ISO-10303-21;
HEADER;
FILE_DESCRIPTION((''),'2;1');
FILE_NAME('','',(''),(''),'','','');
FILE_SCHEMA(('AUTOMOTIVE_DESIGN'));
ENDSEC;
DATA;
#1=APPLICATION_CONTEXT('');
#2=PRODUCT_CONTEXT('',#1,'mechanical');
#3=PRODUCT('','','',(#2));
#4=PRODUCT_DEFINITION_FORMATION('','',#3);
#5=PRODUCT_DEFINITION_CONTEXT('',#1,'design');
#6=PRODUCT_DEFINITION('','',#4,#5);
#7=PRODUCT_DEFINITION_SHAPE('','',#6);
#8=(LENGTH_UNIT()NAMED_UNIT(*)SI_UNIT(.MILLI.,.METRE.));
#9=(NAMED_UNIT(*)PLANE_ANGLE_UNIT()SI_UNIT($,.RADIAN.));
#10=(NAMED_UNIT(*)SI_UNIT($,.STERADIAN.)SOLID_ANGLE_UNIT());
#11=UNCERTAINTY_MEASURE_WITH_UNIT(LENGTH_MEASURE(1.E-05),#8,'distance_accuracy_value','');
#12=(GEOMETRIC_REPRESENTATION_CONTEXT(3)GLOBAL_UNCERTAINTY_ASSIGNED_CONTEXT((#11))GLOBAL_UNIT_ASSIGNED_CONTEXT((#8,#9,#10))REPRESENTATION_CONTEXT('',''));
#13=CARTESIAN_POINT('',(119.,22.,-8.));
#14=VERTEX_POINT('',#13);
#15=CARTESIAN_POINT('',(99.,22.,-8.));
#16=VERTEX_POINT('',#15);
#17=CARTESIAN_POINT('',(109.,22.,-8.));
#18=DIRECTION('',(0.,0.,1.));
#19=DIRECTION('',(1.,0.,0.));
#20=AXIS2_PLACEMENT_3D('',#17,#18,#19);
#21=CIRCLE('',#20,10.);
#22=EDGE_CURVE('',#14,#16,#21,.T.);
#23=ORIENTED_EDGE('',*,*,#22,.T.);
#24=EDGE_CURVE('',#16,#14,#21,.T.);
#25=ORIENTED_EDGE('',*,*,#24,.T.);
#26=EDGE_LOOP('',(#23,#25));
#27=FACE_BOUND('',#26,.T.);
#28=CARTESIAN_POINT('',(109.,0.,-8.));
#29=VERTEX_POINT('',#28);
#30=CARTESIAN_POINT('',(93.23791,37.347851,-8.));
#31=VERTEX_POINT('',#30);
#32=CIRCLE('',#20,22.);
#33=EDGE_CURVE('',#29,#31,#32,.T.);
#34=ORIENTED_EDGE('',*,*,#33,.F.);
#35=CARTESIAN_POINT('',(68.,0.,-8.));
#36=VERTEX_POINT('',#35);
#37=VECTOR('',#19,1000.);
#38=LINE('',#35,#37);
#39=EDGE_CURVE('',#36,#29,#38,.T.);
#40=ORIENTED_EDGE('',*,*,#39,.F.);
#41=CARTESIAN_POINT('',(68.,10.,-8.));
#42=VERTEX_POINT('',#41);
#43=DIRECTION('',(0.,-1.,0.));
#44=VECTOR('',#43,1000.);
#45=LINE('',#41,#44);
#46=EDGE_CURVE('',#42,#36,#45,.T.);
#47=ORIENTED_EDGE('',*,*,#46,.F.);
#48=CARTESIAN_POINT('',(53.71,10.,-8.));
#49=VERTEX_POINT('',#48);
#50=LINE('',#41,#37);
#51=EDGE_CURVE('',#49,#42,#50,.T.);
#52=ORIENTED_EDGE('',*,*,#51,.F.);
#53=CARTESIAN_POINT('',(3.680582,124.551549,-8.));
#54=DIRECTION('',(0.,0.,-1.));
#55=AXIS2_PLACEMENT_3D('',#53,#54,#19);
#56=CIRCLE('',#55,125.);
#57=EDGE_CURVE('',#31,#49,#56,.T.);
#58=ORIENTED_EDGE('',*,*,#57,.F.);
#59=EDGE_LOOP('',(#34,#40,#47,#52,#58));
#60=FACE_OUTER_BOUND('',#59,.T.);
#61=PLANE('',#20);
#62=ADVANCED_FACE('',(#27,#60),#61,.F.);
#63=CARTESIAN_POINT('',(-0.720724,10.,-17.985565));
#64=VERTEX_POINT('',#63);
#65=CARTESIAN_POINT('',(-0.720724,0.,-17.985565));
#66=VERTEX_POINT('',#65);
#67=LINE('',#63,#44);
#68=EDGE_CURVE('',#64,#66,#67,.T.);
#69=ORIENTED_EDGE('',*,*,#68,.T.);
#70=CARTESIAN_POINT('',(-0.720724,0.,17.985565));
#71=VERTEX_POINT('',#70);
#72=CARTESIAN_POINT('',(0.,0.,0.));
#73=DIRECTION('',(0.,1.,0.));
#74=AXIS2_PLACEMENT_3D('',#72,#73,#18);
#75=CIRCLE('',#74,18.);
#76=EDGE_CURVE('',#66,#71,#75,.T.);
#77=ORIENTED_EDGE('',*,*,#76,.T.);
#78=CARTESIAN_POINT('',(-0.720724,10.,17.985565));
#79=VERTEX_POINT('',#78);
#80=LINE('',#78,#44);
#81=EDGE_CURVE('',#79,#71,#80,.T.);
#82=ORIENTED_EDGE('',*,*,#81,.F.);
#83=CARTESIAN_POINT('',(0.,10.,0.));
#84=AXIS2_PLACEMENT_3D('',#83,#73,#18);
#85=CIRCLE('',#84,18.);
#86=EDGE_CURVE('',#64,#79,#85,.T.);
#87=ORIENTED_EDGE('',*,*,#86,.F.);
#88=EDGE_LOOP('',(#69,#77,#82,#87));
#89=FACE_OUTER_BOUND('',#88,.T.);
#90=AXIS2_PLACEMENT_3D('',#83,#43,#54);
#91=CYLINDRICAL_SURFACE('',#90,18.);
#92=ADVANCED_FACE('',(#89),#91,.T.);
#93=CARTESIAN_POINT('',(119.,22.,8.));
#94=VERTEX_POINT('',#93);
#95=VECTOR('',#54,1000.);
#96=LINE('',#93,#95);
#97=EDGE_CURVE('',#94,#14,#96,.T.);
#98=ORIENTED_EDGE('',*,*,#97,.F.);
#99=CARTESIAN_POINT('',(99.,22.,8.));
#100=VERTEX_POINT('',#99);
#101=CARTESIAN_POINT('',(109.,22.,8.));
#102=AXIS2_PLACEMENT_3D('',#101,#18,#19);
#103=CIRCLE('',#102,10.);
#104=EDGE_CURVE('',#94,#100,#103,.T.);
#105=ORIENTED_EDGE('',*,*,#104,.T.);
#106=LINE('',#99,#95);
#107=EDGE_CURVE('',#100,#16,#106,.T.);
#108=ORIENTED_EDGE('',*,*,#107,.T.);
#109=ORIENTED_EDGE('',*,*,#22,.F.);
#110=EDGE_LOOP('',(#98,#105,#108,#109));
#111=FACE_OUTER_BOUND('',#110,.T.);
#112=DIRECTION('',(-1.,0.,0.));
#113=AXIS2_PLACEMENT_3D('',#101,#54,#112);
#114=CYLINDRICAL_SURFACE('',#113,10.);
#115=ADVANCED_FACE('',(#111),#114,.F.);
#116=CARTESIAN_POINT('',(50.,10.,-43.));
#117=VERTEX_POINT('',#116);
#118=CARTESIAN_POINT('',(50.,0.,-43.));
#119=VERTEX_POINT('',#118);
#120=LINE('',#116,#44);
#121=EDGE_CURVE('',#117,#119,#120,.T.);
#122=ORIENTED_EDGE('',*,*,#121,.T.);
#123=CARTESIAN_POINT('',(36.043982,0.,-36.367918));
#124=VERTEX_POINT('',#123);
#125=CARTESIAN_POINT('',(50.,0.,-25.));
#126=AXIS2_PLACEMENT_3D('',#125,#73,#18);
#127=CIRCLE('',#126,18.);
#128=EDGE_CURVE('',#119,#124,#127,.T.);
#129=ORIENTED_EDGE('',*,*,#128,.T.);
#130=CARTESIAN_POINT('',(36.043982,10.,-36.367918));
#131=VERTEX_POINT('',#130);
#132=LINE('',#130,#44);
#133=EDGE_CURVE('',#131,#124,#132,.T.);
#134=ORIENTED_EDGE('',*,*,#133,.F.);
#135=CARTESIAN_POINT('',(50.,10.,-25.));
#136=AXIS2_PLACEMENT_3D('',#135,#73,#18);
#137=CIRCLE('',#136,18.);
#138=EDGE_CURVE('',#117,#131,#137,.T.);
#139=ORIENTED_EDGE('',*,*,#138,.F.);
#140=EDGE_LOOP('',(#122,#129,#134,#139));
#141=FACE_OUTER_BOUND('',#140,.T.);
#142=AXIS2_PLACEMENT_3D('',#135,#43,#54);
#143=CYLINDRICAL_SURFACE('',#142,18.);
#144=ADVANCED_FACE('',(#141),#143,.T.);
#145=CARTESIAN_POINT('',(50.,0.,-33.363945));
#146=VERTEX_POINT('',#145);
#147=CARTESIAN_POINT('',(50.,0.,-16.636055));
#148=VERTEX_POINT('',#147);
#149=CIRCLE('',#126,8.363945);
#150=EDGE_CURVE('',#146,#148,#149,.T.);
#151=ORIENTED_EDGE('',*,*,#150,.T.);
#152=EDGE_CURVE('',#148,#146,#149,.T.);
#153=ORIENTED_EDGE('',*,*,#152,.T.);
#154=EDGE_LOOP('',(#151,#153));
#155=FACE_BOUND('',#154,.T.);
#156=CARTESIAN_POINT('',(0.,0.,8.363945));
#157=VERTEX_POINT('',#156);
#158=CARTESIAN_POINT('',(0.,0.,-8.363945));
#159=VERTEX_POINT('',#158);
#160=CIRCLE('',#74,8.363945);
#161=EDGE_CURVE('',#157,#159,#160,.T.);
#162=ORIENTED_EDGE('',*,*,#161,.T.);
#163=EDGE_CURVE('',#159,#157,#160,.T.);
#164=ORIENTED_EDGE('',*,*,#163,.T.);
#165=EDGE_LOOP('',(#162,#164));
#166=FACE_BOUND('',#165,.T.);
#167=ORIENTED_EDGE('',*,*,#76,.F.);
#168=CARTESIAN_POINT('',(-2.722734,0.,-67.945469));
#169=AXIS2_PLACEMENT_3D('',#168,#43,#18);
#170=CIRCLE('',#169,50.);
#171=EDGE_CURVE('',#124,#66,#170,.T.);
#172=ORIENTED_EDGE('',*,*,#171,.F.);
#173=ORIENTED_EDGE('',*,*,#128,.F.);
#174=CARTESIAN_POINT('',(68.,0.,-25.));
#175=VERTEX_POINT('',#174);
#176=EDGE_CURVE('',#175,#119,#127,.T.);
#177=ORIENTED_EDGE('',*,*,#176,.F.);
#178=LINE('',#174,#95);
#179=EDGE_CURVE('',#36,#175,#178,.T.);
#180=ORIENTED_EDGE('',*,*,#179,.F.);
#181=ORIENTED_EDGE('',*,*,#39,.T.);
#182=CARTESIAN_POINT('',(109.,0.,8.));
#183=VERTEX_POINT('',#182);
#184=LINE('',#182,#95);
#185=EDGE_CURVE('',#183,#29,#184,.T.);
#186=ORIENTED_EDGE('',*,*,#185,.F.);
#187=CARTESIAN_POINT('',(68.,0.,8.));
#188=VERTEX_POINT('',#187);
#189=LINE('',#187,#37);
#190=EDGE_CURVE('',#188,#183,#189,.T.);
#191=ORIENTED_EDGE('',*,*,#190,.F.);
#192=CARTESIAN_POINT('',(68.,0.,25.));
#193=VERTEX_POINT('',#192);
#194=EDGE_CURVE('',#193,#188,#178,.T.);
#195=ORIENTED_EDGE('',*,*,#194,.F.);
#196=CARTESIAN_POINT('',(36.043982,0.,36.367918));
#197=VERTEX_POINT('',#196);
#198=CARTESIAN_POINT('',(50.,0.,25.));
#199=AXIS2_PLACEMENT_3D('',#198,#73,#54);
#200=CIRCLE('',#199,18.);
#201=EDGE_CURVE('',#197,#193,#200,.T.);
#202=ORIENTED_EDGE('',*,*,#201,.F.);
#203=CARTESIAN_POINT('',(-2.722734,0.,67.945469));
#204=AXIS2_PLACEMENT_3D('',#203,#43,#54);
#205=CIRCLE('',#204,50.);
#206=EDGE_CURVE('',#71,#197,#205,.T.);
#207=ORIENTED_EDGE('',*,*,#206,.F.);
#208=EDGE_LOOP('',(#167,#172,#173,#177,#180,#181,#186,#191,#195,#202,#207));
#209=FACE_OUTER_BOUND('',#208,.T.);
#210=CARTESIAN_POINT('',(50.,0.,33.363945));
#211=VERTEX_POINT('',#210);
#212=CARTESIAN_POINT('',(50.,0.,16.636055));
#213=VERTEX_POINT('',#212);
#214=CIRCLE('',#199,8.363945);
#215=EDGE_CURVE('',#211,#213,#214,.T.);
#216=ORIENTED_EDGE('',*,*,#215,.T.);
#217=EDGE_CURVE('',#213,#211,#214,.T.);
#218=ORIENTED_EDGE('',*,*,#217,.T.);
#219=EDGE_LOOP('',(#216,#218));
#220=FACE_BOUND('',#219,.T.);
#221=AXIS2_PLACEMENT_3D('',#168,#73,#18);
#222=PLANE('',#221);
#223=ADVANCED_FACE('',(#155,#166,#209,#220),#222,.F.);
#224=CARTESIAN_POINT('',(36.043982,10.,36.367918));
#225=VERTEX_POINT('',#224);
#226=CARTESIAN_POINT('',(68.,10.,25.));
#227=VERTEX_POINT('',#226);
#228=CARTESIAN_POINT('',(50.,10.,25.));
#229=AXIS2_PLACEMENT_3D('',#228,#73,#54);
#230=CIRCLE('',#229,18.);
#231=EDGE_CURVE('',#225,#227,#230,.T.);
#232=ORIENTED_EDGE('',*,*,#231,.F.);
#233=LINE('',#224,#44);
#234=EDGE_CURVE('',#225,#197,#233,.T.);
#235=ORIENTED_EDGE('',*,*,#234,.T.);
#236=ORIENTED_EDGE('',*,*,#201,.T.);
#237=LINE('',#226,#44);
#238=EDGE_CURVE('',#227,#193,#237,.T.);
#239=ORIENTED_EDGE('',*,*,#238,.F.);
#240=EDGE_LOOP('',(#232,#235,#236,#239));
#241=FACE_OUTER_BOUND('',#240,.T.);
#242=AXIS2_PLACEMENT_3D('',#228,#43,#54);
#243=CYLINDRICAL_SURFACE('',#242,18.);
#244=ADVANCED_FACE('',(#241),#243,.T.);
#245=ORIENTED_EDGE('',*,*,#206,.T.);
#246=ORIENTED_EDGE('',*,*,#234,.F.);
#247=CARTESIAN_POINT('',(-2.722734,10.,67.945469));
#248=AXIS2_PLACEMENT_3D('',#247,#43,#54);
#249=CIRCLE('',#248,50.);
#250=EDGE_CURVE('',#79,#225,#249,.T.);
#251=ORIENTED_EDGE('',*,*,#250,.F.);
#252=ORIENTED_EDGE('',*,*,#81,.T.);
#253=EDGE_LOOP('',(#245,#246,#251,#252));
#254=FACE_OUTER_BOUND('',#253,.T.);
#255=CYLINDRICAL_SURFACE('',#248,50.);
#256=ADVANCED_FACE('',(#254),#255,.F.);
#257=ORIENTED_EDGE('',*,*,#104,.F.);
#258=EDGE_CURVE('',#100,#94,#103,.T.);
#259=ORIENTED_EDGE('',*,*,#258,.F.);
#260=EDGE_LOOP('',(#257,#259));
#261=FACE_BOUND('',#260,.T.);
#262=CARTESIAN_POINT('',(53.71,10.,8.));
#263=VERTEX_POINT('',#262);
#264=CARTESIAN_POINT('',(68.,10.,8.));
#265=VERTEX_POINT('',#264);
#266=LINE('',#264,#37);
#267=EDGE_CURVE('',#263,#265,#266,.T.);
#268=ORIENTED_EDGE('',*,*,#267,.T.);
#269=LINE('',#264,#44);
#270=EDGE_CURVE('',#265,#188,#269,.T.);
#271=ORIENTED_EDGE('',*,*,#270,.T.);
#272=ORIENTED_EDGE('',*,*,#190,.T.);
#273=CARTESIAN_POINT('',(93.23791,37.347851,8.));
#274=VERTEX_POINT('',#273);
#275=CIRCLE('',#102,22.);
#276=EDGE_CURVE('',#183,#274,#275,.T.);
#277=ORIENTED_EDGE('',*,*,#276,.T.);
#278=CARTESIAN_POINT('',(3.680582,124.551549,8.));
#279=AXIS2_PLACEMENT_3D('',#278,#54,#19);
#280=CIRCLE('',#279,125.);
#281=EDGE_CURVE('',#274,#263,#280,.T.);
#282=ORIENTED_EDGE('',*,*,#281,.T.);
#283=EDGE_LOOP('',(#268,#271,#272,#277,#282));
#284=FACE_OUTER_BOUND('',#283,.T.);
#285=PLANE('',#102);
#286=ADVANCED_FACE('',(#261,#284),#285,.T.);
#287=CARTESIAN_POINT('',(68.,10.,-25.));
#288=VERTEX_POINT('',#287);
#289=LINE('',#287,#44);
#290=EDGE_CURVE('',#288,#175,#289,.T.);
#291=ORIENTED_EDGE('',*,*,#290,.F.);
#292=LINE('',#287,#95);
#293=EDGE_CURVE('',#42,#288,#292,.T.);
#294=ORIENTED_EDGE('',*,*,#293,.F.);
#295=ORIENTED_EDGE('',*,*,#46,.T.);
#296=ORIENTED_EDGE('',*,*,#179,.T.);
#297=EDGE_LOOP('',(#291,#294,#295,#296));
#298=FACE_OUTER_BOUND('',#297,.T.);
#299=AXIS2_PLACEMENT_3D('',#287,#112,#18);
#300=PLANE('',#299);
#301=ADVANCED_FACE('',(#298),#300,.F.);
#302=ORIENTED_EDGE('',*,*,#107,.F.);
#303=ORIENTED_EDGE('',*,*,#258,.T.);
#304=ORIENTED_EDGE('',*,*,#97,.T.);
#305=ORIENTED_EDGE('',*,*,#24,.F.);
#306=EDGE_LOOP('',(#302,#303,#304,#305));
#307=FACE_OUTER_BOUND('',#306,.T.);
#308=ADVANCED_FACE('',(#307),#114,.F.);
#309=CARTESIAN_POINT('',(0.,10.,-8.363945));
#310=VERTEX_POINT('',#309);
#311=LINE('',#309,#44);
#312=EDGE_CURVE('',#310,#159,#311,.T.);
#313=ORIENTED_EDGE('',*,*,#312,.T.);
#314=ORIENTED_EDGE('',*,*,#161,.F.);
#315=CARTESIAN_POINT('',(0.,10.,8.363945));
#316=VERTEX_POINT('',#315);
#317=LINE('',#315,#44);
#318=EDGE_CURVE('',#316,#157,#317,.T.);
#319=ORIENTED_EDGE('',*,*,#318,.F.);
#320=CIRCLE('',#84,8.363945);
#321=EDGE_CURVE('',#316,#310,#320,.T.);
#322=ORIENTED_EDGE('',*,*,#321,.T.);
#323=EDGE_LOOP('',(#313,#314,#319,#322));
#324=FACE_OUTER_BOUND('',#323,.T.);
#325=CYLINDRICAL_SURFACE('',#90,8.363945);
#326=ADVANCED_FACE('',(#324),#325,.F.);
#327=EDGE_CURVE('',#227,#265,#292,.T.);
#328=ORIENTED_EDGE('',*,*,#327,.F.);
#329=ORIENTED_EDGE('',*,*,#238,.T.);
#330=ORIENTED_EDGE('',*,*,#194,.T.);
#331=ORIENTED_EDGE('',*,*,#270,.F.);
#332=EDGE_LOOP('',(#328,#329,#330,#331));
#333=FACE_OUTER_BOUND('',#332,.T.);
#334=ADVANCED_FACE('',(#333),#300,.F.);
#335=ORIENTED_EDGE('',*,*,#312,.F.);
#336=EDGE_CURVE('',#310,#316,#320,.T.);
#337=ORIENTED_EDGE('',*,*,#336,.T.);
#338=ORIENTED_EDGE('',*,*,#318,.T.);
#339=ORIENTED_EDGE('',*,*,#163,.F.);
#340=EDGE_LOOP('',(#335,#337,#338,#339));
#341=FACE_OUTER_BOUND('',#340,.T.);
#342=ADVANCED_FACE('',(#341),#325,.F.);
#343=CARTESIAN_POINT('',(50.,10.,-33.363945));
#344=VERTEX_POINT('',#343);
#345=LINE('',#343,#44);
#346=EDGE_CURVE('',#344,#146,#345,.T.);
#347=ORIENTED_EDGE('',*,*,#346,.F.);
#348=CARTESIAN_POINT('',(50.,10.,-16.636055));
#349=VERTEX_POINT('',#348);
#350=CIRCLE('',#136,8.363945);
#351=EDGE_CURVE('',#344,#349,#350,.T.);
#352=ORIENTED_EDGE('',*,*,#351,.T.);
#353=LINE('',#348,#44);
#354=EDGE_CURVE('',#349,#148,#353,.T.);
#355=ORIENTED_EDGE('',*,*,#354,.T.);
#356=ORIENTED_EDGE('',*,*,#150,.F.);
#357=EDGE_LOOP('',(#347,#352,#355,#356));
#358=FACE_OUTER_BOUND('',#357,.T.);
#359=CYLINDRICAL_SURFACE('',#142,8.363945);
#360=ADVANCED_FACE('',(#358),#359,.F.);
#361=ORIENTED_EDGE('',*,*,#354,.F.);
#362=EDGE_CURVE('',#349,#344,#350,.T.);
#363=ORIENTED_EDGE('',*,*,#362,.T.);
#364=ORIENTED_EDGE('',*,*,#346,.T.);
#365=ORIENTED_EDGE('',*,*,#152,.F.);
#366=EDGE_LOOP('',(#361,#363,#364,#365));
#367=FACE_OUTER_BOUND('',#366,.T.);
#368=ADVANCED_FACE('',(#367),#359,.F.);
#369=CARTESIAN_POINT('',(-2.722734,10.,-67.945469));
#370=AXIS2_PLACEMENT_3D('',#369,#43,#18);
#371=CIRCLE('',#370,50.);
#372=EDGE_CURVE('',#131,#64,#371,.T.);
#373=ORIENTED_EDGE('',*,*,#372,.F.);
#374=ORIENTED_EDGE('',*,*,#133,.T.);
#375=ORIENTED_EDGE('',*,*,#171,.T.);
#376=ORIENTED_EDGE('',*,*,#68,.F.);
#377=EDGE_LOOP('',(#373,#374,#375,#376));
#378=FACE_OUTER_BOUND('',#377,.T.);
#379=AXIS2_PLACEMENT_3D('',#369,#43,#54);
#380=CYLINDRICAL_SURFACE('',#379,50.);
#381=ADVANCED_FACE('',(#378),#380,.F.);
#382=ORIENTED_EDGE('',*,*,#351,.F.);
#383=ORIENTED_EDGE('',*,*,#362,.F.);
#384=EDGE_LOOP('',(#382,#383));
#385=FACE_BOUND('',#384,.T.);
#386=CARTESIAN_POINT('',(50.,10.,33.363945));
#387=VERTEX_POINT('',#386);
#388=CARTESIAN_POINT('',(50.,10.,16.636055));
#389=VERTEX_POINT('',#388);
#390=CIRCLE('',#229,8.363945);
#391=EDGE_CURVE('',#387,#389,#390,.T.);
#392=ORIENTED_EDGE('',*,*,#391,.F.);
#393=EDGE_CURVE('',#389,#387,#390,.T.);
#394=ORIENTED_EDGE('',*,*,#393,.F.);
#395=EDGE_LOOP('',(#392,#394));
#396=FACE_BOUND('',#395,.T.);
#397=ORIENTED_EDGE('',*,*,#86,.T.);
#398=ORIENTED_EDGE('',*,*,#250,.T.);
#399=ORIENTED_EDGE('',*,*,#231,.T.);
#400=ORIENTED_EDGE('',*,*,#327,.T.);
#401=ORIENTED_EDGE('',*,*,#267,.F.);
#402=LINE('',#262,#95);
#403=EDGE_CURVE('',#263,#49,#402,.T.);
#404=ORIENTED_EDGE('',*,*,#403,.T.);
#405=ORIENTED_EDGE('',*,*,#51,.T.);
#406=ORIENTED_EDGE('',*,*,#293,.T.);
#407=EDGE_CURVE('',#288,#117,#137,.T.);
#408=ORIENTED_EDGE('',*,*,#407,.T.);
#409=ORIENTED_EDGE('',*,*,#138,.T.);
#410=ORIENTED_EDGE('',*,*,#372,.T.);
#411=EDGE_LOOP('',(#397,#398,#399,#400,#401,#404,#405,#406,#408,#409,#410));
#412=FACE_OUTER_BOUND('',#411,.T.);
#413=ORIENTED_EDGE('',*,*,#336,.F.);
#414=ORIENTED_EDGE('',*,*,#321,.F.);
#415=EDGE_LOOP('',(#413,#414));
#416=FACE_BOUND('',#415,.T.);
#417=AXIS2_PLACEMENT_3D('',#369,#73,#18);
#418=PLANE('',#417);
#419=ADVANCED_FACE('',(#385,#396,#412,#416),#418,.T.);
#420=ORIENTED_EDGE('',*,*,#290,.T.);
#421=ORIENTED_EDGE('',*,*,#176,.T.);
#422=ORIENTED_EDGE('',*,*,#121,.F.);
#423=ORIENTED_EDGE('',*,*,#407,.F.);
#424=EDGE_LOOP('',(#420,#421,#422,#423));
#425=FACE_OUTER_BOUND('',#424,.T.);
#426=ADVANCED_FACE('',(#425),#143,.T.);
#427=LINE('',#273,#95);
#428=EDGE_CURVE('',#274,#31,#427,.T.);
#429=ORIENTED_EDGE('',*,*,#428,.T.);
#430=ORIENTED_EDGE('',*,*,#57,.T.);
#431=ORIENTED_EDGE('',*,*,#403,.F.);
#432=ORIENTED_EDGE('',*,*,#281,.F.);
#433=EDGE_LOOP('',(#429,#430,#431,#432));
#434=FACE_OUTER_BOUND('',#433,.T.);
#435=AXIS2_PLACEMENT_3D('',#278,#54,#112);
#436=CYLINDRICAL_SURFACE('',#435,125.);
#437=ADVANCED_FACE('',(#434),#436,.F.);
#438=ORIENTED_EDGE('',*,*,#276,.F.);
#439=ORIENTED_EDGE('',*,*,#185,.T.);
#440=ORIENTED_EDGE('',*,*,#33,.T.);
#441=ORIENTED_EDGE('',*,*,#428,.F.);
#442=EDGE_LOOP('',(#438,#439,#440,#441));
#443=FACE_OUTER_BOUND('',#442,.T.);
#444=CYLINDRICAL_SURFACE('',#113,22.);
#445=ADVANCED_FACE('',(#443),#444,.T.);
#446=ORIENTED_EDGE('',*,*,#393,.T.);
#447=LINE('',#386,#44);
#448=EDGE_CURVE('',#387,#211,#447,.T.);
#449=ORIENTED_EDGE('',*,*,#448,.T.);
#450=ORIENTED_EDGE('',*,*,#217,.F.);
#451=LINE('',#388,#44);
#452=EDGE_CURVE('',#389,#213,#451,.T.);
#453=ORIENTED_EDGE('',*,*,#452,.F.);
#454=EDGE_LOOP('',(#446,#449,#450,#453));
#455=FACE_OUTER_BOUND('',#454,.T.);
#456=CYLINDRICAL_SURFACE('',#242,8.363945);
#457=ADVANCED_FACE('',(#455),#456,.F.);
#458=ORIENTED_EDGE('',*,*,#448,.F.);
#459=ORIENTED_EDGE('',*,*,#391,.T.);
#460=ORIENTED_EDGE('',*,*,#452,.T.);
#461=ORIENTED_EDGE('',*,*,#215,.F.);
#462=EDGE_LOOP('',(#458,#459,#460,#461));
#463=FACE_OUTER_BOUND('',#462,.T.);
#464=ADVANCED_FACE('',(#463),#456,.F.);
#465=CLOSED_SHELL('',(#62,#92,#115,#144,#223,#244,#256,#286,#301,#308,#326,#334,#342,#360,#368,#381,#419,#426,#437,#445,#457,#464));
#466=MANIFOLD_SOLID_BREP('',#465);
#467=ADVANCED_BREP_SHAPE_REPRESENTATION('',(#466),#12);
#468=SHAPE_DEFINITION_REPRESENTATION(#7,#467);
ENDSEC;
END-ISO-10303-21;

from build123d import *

# Parameters (mm, degrees)
BASE_PLATE_PROFILE_SKETCH_R = 8.363945013
BASE_PLATE_3_HOLE_DEPTH     = 10
BORED_LUG_PROFILE_SKETCH_R  = 10
BORED_LUG_DEPTH             = 8


with BuildPart() as part:
    # Base Plate Profile Sketch → Base Plate 3-Hole (new body)
    with BuildSketch(Plane(origin=(0, 0, 0), x_dir=(1, 0, 0), z_dir=(0, 1, 0))):
        with BuildLine():
            Line((68, 25), (68, -25))
            ThreePointArc((68, -25), (56.032896381, -41.958896227), (36.043982083, -36.367918187))
            ThreePointArc((36.043982083, -36.367918187), (19.637945422, -23.224109156), (-0.720723799, -17.985565246))
            ThreePointArc((-0.720723799, -17.985565246), (-18, 0), (-0.720723799, 17.985565246))
            ThreePointArc((-0.720723799, 17.985565246), (19.637945422, 23.224109156), (36.043982083, 36.367918187))
            ThreePointArc((36.043982083, 36.367918187), (56.032896381, 41.958896227), (68, 25))
        make_face()
        with Locations(Location((0, 0, 0), (0, 0, 270))):
            Circle(BASE_PLATE_PROFILE_SKETCH_R, mode=Mode.SUBTRACT)
        with Locations(Location((50, 25, 0), (0, 0, 270))):
            Circle(BASE_PLATE_PROFILE_SKETCH_R, mode=Mode.SUBTRACT)
        with Locations(Location((50, -25, 0), (0, 0, 90))):
            Circle(BASE_PLATE_PROFILE_SKETCH_R, mode=Mode.SUBTRACT)
    extrude(amount=BASE_PLATE_3_HOLE_DEPTH)

    # Bored Lug Profile Sketch → Bored Lug (add, symmetric)
    with BuildSketch(Plane.XY):
        with BuildLine():
            Line((68, 10), (53.71, 10))
            ThreePointArc((53.71, 10), (74.800840464, 21.756077977), (93.237910195, 37.347850827))
            ThreePointArc((93.237910195, 37.347850827), (129.268851943, 30.554159275), (109, 0))
            Line((109, 0), (68, 0))
            Line((68, 0), (68, 10))
        make_face()
        with Locations((109, 22)):
            Circle(BORED_LUG_PROFILE_SKETCH_R, mode=Mode.SUBTRACT)
    extrude(amount=BORED_LUG_DEPTH, both=True)


solid = part.part
